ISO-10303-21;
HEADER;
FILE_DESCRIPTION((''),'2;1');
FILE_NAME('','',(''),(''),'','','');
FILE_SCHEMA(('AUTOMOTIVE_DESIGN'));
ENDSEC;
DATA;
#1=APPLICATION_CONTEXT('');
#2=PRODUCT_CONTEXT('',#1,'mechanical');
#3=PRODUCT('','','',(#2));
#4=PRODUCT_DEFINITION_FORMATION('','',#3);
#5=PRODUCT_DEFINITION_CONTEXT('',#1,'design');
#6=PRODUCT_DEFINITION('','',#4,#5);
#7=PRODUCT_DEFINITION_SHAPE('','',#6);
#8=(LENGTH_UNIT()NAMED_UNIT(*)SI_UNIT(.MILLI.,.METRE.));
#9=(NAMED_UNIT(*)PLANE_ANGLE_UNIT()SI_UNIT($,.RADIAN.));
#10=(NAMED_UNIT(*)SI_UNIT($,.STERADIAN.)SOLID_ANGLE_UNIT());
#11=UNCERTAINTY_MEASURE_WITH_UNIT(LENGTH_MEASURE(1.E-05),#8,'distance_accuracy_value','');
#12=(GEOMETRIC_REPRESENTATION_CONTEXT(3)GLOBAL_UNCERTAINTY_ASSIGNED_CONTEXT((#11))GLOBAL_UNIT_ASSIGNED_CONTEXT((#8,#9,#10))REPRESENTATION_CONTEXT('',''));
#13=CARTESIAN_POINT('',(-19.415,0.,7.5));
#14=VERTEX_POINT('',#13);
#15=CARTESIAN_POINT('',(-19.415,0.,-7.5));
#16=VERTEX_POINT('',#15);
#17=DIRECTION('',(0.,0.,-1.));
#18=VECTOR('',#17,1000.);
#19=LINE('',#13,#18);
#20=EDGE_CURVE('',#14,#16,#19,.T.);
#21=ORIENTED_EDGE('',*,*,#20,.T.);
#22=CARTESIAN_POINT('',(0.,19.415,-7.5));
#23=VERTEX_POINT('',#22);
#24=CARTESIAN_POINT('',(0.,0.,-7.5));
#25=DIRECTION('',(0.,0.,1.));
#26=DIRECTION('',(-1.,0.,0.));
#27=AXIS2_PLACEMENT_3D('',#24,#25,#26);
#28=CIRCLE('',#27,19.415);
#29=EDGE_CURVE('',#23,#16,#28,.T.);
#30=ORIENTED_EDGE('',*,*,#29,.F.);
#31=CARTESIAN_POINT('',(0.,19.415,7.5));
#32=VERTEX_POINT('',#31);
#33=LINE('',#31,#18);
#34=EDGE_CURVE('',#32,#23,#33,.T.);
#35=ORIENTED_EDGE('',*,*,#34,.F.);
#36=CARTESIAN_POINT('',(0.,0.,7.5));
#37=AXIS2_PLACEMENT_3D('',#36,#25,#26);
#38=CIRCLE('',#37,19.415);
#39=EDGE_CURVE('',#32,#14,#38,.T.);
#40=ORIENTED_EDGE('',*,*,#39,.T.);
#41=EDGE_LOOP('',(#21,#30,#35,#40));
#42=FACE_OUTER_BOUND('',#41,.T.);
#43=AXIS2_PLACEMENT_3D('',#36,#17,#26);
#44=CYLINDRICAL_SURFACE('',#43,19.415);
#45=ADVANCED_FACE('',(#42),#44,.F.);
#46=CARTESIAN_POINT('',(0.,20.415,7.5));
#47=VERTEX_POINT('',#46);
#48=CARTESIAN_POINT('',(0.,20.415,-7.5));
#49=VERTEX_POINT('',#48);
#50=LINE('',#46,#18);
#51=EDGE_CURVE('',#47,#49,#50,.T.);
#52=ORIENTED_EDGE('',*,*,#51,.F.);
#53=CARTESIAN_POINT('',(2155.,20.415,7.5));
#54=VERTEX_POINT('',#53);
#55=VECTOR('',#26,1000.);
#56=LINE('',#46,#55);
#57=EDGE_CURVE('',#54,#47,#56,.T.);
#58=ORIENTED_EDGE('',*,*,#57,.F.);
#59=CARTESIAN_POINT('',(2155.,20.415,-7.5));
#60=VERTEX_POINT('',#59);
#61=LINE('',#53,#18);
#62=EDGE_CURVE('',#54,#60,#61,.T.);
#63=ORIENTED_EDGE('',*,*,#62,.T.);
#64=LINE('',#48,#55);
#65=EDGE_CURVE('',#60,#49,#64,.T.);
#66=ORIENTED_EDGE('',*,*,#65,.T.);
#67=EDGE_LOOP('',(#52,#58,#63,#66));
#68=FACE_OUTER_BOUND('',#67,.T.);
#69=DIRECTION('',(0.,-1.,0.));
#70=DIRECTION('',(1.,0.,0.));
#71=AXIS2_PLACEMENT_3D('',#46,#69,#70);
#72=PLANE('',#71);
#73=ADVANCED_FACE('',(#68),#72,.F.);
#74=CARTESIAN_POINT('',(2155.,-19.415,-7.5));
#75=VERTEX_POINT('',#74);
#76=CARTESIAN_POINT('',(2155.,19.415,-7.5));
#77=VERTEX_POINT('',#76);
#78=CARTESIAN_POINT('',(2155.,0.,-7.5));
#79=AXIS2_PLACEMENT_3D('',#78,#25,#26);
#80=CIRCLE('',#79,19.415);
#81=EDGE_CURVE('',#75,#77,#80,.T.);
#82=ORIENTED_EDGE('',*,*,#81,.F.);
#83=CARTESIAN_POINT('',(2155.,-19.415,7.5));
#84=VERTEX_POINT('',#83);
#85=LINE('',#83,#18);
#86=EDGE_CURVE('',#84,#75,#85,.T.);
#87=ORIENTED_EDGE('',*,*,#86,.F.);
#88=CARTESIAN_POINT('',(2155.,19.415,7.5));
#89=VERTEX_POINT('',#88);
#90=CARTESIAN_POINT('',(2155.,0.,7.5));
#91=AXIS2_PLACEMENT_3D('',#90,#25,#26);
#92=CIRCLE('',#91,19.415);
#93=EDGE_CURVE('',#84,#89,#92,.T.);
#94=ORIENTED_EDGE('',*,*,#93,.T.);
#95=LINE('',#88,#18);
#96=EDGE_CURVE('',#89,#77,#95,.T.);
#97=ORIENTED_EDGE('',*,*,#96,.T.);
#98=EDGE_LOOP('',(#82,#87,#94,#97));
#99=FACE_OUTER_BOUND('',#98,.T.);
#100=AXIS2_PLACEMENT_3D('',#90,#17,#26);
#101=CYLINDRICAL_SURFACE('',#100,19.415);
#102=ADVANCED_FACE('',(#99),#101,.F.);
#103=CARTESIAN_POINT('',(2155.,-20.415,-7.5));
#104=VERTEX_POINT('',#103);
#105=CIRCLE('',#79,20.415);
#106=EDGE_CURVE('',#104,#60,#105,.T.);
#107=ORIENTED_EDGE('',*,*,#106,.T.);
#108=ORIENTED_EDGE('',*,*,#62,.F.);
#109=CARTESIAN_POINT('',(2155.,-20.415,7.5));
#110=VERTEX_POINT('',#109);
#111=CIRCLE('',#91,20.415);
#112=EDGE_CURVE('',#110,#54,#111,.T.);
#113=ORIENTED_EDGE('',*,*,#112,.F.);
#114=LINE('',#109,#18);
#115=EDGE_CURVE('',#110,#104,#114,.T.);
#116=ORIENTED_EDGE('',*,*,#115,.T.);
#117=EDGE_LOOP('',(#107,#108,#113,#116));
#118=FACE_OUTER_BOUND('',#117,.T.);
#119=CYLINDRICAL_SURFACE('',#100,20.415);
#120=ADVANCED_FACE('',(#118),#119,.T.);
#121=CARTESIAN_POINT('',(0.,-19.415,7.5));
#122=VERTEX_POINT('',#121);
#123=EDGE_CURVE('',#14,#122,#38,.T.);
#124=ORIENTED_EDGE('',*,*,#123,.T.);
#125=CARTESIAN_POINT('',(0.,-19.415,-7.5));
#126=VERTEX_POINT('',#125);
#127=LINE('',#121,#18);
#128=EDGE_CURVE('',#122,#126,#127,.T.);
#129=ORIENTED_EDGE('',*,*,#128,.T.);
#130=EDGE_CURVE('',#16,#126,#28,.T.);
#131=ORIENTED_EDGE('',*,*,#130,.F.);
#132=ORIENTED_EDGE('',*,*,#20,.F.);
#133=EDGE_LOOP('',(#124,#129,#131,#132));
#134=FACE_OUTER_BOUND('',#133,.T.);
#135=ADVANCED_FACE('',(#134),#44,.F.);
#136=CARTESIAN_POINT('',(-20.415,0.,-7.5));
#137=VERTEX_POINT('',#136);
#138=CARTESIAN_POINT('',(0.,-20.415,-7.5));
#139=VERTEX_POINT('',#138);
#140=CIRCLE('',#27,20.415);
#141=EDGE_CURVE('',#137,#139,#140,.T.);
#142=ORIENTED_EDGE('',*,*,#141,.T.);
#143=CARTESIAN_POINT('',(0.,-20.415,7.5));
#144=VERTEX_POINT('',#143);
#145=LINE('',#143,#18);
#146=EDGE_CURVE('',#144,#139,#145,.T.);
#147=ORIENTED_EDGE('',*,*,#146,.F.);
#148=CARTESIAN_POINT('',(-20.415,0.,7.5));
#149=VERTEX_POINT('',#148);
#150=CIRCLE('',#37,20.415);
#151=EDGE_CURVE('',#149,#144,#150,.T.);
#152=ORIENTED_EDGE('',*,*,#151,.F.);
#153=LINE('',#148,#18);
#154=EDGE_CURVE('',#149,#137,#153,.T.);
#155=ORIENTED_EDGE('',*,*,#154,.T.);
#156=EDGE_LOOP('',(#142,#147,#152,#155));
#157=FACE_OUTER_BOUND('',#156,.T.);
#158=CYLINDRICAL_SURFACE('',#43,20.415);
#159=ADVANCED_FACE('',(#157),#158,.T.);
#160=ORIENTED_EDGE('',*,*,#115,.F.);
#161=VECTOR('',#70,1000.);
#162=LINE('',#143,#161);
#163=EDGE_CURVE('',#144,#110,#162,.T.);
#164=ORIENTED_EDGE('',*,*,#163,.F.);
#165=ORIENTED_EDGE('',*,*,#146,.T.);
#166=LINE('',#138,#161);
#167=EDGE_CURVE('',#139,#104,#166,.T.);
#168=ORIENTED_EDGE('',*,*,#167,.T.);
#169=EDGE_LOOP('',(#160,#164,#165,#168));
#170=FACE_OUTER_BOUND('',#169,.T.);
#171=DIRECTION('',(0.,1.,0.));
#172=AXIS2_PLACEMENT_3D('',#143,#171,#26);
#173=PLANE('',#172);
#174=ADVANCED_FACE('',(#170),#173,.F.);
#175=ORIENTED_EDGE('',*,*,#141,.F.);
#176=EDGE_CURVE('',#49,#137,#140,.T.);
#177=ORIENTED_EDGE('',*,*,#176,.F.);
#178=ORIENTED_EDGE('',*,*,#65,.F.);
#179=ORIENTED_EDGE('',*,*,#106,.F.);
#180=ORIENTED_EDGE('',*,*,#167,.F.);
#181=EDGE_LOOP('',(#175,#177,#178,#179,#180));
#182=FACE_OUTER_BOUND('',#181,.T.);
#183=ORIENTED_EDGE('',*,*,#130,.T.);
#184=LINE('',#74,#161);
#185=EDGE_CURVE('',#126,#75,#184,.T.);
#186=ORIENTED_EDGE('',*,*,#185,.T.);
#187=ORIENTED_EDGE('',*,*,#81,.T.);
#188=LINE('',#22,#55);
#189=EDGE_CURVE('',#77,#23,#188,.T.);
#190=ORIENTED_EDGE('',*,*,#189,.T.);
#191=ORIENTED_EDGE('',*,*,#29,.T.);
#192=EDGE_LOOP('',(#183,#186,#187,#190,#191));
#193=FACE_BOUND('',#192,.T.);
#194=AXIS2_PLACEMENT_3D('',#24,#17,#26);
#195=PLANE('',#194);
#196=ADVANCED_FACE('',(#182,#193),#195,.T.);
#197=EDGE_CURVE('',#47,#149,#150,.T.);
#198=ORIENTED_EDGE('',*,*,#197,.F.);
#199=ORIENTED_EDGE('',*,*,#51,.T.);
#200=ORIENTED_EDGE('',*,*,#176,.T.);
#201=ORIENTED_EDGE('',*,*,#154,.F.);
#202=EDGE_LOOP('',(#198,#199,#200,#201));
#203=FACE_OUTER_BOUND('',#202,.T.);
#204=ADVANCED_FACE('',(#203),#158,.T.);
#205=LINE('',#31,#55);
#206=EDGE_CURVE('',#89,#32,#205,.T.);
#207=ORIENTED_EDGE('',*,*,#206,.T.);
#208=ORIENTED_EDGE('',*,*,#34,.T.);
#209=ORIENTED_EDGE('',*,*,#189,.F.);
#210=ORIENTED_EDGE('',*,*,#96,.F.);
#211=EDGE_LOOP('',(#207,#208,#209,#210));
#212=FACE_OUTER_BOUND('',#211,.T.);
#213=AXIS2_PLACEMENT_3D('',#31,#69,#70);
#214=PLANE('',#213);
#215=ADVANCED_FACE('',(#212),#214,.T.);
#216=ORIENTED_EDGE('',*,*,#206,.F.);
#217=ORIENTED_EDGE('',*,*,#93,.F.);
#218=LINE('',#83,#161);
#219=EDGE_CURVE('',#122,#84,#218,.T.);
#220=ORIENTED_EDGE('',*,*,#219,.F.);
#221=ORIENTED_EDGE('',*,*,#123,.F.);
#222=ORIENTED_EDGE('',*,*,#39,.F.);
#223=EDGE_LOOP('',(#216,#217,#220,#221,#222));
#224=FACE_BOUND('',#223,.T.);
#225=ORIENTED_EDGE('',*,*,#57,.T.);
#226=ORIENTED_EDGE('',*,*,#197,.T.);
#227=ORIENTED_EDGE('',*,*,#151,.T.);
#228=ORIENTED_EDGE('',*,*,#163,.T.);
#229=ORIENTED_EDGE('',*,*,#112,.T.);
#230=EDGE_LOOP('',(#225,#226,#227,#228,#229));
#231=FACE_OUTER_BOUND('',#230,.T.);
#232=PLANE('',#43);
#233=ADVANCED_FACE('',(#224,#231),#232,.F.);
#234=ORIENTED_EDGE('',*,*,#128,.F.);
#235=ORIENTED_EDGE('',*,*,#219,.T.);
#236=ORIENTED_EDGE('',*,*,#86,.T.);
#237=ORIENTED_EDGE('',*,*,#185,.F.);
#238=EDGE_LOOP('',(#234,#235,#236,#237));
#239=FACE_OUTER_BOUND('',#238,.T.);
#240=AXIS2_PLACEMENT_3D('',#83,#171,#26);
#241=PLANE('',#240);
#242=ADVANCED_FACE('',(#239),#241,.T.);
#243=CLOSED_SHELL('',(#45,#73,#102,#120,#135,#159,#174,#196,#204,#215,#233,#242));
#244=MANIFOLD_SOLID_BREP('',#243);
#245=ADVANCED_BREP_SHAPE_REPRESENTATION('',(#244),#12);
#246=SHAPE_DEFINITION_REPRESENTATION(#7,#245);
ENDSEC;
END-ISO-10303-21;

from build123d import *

# Parameters (mm, degrees)
EXTRUDE_1_DEPTH = 7.5


with BuildPart() as part:
    # 草图2 → 拉伸-薄壁1 (new, symmetric)
    with BuildSketch(Plane.XY):
        with BuildLine():
            Line((2155, -20.415), (0, -20.415))
            ThreePointArc((0, -20.415), (-20.415, 0), (0, 20.415))
            Line((0, 20.415), (2155, 20.415))
            ThreePointArc((2155, 20.415), (2175.415, 0), (2155, -20.415))
        make_face()
        with BuildLine():
            Line((2155, -19.415), (0, -19.415))
            ThreePointArc((0, -19.415), (-19.415, 0), (0, 19.415))
            Line((0, 19.415), (2155, 19.415))
            ThreePointArc((2155, 19.415), (2174.415, 0), (2155, -19.415))
        make_face(mode=Mode.SUBTRACT)
    extrude(amount=EXTRUDE_1_DEPTH, both=True)


solid = part.part
